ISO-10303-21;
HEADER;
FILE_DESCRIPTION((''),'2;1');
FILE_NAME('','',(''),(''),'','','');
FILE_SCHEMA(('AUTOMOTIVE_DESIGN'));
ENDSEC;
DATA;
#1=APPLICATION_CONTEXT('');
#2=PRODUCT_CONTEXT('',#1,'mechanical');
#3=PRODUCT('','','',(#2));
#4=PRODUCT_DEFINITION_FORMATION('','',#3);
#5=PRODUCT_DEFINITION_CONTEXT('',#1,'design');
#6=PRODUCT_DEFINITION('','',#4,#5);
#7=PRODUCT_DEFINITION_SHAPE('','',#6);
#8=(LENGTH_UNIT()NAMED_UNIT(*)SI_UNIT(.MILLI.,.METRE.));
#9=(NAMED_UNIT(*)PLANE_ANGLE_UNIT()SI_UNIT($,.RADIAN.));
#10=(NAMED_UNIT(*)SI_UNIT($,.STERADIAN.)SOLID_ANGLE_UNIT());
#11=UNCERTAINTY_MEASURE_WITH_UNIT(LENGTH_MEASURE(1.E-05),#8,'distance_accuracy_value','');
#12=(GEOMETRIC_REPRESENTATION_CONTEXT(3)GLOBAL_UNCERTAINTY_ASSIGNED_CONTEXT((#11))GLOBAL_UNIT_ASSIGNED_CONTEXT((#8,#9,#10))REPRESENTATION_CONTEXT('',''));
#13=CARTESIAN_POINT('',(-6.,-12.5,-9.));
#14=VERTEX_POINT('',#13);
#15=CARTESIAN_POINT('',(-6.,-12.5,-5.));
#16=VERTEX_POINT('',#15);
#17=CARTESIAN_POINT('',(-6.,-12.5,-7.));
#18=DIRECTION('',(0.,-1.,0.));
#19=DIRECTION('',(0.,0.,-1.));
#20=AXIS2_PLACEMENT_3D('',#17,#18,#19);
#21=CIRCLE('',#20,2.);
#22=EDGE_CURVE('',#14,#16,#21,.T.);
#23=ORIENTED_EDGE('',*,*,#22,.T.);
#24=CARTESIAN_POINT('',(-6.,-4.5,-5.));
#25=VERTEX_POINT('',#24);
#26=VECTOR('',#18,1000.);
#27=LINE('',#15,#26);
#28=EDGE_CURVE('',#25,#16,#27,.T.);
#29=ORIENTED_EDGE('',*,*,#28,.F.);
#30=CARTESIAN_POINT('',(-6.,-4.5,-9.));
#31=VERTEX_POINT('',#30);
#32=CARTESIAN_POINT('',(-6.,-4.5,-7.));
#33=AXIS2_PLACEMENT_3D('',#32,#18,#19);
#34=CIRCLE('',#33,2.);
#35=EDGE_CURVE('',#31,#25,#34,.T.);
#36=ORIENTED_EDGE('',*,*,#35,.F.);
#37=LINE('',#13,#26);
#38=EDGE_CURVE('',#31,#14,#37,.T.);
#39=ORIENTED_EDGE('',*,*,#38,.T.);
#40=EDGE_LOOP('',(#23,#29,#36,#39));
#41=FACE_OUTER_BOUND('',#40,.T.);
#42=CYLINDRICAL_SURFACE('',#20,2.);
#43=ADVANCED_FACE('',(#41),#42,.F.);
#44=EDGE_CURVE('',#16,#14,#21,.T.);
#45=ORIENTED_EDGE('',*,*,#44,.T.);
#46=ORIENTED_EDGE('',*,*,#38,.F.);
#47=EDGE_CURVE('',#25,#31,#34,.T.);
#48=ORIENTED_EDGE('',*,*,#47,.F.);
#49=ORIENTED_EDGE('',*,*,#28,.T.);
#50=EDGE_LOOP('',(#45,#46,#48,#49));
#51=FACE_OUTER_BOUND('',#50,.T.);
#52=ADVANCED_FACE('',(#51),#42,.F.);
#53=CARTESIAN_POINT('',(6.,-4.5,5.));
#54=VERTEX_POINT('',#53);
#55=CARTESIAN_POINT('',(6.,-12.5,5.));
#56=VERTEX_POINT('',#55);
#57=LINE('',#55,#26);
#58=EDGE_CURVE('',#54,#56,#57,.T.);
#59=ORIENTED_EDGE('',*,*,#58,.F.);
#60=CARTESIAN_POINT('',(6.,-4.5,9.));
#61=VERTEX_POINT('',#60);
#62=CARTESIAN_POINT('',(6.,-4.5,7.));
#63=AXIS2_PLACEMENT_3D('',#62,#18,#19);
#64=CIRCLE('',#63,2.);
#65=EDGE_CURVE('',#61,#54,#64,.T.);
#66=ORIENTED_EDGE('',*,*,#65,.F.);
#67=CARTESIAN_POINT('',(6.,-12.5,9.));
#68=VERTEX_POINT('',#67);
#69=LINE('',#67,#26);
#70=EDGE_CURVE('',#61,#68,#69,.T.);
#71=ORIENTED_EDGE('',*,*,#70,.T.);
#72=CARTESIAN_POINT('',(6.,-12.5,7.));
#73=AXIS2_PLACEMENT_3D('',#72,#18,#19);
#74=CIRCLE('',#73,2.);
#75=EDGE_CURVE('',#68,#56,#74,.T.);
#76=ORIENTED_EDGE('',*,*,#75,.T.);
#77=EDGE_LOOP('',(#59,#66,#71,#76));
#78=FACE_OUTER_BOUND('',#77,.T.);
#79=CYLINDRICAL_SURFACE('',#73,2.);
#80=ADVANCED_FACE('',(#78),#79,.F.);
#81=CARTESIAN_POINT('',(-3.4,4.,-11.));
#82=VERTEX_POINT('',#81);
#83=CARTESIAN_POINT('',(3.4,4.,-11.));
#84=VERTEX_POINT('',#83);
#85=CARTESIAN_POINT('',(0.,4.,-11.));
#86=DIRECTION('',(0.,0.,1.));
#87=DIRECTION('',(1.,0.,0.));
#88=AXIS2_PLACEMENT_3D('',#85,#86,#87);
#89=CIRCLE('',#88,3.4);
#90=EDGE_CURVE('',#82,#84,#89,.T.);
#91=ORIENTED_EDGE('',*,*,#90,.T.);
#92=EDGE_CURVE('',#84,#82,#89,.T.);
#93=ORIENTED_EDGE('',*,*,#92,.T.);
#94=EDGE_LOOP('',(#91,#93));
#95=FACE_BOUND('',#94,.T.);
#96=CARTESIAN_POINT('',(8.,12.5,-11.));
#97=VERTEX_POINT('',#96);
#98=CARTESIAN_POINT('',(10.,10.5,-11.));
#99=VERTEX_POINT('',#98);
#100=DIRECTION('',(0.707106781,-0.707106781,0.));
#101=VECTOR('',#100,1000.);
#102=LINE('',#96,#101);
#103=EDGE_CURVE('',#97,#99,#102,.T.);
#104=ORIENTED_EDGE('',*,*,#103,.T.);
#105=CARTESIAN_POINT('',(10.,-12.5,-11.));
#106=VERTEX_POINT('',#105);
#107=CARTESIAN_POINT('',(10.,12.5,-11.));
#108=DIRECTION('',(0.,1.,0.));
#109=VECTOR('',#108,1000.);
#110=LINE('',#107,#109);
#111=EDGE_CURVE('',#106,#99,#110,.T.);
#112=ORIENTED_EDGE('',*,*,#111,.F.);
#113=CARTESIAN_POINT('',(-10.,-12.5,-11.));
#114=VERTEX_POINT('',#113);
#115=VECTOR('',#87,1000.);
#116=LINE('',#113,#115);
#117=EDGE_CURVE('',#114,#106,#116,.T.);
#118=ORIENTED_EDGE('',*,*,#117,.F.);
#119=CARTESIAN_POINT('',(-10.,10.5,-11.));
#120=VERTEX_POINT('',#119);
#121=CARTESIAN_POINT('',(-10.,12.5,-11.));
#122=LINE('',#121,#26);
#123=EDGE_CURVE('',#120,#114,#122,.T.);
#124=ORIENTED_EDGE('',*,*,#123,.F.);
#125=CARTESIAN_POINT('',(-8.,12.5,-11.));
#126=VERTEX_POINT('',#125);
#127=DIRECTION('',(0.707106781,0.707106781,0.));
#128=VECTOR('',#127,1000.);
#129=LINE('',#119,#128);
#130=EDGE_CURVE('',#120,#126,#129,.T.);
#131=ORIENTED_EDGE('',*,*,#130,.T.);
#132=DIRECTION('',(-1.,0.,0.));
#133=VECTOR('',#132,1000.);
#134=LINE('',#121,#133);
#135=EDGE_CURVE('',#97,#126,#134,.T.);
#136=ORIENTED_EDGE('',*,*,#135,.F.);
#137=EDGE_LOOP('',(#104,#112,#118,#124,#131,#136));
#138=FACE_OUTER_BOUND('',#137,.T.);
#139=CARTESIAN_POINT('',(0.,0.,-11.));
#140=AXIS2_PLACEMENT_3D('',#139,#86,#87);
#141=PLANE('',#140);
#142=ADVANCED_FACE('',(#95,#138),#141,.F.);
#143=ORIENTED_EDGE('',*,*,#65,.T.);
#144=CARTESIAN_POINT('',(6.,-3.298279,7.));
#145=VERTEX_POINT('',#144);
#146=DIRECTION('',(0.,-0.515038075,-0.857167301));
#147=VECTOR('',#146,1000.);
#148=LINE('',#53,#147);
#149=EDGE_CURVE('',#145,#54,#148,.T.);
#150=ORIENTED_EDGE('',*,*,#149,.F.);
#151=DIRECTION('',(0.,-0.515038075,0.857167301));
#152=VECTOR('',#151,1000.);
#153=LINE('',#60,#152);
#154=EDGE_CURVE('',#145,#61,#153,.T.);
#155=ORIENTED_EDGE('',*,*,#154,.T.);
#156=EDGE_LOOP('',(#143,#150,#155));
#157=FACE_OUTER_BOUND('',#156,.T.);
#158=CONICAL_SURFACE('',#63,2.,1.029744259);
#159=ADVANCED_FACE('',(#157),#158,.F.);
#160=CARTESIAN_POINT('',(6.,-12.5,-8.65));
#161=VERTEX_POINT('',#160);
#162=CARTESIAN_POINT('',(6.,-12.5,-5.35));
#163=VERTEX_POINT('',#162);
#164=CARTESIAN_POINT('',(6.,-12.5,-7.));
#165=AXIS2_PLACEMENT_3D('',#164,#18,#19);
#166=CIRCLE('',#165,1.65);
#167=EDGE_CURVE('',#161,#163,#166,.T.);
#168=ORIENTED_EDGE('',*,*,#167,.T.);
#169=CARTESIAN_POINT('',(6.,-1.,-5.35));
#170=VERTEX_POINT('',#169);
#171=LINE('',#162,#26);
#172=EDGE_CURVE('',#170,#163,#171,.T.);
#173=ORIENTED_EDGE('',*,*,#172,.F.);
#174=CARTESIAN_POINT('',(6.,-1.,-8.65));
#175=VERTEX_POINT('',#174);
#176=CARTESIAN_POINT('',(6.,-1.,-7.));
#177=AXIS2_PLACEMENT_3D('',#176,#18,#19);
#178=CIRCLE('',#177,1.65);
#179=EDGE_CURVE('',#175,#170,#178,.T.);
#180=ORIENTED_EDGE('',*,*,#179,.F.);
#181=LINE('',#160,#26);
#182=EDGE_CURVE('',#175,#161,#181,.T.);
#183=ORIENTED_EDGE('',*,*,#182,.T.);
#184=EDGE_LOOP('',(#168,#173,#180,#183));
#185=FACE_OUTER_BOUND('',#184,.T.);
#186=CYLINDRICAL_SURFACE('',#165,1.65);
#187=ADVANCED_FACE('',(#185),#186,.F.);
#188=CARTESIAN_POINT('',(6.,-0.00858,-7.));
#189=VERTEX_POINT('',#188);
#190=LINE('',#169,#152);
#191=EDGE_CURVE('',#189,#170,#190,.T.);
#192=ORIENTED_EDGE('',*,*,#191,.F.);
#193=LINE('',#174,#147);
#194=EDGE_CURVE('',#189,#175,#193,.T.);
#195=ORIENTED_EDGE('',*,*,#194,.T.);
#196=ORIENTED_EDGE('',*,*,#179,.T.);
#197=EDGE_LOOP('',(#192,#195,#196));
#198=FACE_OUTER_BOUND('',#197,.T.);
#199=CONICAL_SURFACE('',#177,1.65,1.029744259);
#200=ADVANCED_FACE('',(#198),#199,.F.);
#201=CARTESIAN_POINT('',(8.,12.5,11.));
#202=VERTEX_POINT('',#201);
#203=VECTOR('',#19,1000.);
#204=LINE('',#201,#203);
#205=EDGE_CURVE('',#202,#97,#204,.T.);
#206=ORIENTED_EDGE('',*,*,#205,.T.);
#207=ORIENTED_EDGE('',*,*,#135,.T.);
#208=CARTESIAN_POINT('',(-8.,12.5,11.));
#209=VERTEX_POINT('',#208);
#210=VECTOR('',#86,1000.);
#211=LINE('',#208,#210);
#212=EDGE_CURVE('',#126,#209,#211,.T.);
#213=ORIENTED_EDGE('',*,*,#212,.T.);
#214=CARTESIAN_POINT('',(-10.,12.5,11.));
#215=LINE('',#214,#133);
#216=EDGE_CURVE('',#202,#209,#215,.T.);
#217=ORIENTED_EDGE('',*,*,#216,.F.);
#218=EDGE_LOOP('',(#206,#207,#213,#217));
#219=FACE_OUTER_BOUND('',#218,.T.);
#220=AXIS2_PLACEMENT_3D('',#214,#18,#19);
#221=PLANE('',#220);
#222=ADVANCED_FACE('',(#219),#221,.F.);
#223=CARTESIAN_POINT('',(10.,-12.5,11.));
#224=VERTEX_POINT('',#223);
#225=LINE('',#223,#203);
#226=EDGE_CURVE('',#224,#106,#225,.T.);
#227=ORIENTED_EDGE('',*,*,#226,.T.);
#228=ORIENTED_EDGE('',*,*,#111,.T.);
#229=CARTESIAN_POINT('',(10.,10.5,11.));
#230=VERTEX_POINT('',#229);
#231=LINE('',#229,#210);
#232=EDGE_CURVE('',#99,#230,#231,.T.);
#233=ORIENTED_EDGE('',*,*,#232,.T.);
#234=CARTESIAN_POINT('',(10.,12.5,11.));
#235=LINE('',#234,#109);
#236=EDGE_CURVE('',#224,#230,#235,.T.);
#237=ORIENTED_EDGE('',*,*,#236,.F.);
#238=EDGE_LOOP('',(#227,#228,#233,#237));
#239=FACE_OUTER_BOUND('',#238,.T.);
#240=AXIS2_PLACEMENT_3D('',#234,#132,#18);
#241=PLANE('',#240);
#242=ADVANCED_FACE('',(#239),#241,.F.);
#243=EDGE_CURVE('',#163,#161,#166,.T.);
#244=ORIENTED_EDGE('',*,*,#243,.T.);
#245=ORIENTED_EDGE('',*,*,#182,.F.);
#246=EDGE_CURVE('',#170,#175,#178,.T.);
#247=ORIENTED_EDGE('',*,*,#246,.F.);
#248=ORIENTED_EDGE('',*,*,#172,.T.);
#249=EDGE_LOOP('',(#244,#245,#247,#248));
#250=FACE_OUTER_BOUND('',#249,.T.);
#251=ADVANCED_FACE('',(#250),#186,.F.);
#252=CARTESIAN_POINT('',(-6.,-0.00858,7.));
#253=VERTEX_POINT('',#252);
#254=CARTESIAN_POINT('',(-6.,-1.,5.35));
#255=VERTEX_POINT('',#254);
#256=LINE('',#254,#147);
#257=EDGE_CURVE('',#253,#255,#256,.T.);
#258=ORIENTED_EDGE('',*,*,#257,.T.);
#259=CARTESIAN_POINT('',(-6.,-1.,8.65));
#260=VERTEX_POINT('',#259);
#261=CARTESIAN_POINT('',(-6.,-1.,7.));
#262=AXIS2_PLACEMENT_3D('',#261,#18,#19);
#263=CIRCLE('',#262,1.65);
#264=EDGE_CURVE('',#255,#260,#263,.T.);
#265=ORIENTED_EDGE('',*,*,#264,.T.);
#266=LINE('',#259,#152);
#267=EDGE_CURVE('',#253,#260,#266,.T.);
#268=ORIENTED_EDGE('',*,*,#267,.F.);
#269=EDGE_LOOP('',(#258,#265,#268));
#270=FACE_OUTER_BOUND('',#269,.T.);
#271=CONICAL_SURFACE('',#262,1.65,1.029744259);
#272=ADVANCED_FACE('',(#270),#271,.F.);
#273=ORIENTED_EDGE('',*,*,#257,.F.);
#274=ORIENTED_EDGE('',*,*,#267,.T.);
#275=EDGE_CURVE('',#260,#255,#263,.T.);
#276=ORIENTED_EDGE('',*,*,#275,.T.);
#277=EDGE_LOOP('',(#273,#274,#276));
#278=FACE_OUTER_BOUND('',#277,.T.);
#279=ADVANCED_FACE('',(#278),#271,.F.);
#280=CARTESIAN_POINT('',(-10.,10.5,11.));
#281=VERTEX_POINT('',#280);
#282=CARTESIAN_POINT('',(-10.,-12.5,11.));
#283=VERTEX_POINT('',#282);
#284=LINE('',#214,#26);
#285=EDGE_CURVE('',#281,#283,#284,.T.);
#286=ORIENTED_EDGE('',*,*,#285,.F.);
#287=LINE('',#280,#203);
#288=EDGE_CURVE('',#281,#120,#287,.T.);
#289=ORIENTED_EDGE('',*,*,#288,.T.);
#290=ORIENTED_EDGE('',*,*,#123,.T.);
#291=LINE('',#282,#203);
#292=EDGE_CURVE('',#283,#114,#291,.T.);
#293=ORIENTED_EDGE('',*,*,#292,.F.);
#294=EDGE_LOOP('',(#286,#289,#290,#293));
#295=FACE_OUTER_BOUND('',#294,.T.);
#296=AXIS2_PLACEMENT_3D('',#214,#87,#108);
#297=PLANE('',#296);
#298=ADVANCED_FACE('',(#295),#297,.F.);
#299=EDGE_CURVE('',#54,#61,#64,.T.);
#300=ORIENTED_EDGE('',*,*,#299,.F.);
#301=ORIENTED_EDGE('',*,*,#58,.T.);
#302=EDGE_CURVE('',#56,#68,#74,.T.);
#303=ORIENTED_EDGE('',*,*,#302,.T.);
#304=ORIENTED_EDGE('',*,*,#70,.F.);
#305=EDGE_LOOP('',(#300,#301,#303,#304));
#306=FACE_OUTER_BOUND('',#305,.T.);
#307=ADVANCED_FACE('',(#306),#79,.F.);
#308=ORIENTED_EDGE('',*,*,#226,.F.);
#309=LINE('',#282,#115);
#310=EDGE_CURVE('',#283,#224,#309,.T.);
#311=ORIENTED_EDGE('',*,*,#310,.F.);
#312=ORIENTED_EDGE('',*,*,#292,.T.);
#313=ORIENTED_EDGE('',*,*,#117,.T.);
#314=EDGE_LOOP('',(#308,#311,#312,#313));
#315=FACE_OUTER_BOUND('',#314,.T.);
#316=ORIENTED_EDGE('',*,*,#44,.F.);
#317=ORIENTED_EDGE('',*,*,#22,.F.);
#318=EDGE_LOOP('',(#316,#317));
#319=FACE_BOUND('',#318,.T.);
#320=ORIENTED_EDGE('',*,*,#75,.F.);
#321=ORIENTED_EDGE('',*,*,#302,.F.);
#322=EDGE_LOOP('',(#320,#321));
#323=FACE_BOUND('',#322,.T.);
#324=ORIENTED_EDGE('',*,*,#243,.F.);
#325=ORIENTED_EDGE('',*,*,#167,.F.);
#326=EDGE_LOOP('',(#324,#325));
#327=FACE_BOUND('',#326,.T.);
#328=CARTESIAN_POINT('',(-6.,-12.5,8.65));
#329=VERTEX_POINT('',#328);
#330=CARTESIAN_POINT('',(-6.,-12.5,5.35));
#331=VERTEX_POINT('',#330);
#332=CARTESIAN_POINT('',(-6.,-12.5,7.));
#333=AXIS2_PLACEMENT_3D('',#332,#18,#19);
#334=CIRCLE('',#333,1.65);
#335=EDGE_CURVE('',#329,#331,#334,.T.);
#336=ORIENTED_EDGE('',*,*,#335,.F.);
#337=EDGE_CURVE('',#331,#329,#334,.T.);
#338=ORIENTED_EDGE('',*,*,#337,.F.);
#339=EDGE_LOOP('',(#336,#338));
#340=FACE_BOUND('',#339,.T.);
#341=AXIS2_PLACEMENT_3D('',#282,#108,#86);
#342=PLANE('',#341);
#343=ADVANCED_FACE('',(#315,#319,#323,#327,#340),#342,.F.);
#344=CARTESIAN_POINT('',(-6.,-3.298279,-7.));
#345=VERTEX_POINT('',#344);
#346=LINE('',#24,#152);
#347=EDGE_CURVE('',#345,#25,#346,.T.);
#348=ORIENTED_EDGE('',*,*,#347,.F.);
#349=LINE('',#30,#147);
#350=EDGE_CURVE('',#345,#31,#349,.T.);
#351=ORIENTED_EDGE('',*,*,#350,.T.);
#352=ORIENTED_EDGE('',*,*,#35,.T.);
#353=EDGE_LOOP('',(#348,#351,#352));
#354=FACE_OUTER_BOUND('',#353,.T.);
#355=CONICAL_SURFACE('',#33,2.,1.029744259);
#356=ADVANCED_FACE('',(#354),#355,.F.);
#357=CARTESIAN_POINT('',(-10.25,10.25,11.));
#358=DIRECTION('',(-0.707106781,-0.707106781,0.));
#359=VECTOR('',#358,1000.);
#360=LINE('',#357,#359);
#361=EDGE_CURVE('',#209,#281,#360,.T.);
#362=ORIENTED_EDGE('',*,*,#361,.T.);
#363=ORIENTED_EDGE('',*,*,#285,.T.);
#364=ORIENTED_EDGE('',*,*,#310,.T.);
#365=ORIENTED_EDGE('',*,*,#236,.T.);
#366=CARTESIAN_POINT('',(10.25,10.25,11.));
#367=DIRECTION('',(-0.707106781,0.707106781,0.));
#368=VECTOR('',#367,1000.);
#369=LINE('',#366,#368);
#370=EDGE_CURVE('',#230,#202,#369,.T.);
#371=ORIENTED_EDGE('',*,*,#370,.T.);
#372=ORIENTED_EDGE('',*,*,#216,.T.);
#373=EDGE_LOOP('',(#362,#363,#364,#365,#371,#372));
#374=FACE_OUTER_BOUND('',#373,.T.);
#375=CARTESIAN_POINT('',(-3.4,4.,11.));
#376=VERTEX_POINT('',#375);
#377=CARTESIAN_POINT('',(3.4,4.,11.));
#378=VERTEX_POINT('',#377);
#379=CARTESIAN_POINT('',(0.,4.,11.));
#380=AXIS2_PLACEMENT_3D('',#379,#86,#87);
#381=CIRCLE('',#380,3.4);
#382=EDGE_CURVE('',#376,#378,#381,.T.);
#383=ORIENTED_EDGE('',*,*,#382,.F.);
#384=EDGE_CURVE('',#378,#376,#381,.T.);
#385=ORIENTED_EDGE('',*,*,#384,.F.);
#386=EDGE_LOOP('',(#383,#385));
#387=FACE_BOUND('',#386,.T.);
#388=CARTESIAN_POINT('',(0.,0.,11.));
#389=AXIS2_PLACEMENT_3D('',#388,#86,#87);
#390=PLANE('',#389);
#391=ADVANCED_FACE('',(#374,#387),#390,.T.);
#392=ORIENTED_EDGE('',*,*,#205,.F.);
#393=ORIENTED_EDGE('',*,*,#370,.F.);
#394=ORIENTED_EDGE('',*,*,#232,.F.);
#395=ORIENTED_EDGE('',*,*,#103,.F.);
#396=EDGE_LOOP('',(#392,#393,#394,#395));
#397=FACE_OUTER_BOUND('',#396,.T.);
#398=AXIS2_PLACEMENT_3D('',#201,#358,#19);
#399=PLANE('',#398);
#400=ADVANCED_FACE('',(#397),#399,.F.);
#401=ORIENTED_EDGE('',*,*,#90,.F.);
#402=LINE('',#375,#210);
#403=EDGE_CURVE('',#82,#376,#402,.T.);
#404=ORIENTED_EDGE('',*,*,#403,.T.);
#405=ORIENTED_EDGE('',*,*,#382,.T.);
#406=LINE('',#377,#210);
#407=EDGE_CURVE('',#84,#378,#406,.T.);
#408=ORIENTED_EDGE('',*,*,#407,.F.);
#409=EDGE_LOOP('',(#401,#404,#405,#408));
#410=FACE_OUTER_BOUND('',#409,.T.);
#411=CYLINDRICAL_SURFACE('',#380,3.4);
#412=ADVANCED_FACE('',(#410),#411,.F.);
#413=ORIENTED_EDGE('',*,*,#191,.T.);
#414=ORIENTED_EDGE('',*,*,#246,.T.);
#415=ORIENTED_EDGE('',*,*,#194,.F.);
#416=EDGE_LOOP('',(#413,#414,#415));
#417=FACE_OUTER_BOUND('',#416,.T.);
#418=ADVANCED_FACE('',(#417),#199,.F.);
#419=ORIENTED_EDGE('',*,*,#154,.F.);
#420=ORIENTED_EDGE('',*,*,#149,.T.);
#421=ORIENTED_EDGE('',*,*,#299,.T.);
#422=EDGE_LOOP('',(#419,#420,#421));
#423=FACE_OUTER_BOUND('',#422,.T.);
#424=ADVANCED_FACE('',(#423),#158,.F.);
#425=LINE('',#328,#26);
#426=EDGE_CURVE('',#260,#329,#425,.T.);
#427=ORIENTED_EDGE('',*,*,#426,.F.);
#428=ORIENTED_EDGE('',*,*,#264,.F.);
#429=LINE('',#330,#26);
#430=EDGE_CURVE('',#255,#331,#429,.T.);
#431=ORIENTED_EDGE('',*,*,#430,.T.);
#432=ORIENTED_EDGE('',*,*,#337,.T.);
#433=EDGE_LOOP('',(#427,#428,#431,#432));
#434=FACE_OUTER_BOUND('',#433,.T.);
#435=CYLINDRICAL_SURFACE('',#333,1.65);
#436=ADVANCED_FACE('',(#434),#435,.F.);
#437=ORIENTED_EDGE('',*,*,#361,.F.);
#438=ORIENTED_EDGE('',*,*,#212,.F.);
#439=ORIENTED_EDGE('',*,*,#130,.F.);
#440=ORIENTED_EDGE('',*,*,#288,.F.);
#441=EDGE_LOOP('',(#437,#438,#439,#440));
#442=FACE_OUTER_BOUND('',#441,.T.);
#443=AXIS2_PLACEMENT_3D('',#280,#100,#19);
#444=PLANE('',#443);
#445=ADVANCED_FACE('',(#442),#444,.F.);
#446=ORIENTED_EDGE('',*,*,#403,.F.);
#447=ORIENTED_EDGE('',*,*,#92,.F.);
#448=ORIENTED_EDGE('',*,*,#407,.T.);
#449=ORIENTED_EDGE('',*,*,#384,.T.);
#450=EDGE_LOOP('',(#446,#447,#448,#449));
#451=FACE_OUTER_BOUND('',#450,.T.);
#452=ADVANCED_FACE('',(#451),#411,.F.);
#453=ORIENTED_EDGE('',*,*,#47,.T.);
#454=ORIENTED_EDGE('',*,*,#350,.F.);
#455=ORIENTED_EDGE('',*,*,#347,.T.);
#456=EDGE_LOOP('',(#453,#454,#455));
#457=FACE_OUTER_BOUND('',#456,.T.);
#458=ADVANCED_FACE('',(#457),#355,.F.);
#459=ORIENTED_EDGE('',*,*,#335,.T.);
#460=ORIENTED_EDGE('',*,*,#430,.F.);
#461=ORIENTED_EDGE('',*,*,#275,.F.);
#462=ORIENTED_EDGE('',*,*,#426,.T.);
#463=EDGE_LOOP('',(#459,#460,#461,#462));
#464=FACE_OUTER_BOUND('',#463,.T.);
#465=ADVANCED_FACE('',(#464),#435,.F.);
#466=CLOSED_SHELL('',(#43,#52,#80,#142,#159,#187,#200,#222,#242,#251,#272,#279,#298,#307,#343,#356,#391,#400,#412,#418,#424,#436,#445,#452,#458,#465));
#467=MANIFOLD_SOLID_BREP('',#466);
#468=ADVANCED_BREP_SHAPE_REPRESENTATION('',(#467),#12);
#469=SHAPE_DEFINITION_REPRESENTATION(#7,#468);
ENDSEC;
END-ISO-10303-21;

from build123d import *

# Parameters (mm, degrees)
SKETCH1_W                    = 20
SKETCH1_H                    = 25
BOSS_EXTRUDE1_DEPTH          = 11
CHAMFER1_SIZE                = 2
M8_TAPPED_HOLE1_D            = 6.8
M4_TAPPED_HOLE1_D            = 3.3
M4_TAPPED_HOLE1_DEPTH        = 11.5
M4_TAPPED_HOLE1_TIP          = 0.991420021
F_4_0_4_DIAMETER_HOLE1_D     = 4
F_4_0_4_DIAMETER_HOLE1_DEPTH = 8
F_4_0_4_DIAMETER_HOLE1_TIP   = 1.201721238


with BuildPart() as part:
    # Sketch1 → Boss-Extrude1 (new, symmetric)
    with BuildSketch(Plane.XY):
        Rectangle(SKETCH1_W, SKETCH1_H)
    extrude(amount=BOSS_EXTRUDE1_DEPTH, both=True)

    # Chamfer1
    chamfer1_edges = [part.edges().sort_by_distance(p)[0] for p in [
        (-10, 12.5, 0),
        (10, 12.5, 0),
    ]]
    chamfer(chamfer1_edges, length=CHAMFER1_SIZE)

    # M8 Tapped Hole1 (through all)
    with Locations(Plane.XY.offset(11)):
        with Locations((0, 4)):
            Hole(M8_TAPPED_HOLE1_D / 2)

    # M4 Tapped Hole1
    with Locations(Plane(origin=(0, -12.5, 0), x_dir=(-1, 0, 0), z_dir=(0, -1, 0))):
        with Locations((6, -7), (-6, 7)):
            Hole(M4_TAPPED_HOLE1_D / 2, depth=M4_TAPPED_HOLE1_DEPTH)
            with Locations((0, 0, -(M4_TAPPED_HOLE1_DEPTH + M4_TAPPED_HOLE1_TIP / 2))):  # 118° drill point
                Cone(0, M4_TAPPED_HOLE1_D / 2, M4_TAPPED_HOLE1_TIP, mode=Mode.SUBTRACT)

    # Ø4.0 (4) Diameter Hole1
    with Locations(Plane(origin=(0, -12.5, 0), x_dir=(-1, 0, 0), z_dir=(0, -1, 0))):
        with Locations((-6, -7), (6, 7)):
            Hole(F_4_0_4_DIAMETER_HOLE1_D / 2, depth=F_4_0_4_DIAMETER_HOLE1_DEPTH)
            with Locations((0, 0, -(F_4_0_4_DIAMETER_HOLE1_DEPTH + F_4_0_4_DIAMETER_HOLE1_TIP / 2))):  # 118° drill point
                Cone(0, F_4_0_4_DIAMETER_HOLE1_D / 2, F_4_0_4_DIAMETER_HOLE1_TIP, mode=Mode.SUBTRACT)


solid = part.part
